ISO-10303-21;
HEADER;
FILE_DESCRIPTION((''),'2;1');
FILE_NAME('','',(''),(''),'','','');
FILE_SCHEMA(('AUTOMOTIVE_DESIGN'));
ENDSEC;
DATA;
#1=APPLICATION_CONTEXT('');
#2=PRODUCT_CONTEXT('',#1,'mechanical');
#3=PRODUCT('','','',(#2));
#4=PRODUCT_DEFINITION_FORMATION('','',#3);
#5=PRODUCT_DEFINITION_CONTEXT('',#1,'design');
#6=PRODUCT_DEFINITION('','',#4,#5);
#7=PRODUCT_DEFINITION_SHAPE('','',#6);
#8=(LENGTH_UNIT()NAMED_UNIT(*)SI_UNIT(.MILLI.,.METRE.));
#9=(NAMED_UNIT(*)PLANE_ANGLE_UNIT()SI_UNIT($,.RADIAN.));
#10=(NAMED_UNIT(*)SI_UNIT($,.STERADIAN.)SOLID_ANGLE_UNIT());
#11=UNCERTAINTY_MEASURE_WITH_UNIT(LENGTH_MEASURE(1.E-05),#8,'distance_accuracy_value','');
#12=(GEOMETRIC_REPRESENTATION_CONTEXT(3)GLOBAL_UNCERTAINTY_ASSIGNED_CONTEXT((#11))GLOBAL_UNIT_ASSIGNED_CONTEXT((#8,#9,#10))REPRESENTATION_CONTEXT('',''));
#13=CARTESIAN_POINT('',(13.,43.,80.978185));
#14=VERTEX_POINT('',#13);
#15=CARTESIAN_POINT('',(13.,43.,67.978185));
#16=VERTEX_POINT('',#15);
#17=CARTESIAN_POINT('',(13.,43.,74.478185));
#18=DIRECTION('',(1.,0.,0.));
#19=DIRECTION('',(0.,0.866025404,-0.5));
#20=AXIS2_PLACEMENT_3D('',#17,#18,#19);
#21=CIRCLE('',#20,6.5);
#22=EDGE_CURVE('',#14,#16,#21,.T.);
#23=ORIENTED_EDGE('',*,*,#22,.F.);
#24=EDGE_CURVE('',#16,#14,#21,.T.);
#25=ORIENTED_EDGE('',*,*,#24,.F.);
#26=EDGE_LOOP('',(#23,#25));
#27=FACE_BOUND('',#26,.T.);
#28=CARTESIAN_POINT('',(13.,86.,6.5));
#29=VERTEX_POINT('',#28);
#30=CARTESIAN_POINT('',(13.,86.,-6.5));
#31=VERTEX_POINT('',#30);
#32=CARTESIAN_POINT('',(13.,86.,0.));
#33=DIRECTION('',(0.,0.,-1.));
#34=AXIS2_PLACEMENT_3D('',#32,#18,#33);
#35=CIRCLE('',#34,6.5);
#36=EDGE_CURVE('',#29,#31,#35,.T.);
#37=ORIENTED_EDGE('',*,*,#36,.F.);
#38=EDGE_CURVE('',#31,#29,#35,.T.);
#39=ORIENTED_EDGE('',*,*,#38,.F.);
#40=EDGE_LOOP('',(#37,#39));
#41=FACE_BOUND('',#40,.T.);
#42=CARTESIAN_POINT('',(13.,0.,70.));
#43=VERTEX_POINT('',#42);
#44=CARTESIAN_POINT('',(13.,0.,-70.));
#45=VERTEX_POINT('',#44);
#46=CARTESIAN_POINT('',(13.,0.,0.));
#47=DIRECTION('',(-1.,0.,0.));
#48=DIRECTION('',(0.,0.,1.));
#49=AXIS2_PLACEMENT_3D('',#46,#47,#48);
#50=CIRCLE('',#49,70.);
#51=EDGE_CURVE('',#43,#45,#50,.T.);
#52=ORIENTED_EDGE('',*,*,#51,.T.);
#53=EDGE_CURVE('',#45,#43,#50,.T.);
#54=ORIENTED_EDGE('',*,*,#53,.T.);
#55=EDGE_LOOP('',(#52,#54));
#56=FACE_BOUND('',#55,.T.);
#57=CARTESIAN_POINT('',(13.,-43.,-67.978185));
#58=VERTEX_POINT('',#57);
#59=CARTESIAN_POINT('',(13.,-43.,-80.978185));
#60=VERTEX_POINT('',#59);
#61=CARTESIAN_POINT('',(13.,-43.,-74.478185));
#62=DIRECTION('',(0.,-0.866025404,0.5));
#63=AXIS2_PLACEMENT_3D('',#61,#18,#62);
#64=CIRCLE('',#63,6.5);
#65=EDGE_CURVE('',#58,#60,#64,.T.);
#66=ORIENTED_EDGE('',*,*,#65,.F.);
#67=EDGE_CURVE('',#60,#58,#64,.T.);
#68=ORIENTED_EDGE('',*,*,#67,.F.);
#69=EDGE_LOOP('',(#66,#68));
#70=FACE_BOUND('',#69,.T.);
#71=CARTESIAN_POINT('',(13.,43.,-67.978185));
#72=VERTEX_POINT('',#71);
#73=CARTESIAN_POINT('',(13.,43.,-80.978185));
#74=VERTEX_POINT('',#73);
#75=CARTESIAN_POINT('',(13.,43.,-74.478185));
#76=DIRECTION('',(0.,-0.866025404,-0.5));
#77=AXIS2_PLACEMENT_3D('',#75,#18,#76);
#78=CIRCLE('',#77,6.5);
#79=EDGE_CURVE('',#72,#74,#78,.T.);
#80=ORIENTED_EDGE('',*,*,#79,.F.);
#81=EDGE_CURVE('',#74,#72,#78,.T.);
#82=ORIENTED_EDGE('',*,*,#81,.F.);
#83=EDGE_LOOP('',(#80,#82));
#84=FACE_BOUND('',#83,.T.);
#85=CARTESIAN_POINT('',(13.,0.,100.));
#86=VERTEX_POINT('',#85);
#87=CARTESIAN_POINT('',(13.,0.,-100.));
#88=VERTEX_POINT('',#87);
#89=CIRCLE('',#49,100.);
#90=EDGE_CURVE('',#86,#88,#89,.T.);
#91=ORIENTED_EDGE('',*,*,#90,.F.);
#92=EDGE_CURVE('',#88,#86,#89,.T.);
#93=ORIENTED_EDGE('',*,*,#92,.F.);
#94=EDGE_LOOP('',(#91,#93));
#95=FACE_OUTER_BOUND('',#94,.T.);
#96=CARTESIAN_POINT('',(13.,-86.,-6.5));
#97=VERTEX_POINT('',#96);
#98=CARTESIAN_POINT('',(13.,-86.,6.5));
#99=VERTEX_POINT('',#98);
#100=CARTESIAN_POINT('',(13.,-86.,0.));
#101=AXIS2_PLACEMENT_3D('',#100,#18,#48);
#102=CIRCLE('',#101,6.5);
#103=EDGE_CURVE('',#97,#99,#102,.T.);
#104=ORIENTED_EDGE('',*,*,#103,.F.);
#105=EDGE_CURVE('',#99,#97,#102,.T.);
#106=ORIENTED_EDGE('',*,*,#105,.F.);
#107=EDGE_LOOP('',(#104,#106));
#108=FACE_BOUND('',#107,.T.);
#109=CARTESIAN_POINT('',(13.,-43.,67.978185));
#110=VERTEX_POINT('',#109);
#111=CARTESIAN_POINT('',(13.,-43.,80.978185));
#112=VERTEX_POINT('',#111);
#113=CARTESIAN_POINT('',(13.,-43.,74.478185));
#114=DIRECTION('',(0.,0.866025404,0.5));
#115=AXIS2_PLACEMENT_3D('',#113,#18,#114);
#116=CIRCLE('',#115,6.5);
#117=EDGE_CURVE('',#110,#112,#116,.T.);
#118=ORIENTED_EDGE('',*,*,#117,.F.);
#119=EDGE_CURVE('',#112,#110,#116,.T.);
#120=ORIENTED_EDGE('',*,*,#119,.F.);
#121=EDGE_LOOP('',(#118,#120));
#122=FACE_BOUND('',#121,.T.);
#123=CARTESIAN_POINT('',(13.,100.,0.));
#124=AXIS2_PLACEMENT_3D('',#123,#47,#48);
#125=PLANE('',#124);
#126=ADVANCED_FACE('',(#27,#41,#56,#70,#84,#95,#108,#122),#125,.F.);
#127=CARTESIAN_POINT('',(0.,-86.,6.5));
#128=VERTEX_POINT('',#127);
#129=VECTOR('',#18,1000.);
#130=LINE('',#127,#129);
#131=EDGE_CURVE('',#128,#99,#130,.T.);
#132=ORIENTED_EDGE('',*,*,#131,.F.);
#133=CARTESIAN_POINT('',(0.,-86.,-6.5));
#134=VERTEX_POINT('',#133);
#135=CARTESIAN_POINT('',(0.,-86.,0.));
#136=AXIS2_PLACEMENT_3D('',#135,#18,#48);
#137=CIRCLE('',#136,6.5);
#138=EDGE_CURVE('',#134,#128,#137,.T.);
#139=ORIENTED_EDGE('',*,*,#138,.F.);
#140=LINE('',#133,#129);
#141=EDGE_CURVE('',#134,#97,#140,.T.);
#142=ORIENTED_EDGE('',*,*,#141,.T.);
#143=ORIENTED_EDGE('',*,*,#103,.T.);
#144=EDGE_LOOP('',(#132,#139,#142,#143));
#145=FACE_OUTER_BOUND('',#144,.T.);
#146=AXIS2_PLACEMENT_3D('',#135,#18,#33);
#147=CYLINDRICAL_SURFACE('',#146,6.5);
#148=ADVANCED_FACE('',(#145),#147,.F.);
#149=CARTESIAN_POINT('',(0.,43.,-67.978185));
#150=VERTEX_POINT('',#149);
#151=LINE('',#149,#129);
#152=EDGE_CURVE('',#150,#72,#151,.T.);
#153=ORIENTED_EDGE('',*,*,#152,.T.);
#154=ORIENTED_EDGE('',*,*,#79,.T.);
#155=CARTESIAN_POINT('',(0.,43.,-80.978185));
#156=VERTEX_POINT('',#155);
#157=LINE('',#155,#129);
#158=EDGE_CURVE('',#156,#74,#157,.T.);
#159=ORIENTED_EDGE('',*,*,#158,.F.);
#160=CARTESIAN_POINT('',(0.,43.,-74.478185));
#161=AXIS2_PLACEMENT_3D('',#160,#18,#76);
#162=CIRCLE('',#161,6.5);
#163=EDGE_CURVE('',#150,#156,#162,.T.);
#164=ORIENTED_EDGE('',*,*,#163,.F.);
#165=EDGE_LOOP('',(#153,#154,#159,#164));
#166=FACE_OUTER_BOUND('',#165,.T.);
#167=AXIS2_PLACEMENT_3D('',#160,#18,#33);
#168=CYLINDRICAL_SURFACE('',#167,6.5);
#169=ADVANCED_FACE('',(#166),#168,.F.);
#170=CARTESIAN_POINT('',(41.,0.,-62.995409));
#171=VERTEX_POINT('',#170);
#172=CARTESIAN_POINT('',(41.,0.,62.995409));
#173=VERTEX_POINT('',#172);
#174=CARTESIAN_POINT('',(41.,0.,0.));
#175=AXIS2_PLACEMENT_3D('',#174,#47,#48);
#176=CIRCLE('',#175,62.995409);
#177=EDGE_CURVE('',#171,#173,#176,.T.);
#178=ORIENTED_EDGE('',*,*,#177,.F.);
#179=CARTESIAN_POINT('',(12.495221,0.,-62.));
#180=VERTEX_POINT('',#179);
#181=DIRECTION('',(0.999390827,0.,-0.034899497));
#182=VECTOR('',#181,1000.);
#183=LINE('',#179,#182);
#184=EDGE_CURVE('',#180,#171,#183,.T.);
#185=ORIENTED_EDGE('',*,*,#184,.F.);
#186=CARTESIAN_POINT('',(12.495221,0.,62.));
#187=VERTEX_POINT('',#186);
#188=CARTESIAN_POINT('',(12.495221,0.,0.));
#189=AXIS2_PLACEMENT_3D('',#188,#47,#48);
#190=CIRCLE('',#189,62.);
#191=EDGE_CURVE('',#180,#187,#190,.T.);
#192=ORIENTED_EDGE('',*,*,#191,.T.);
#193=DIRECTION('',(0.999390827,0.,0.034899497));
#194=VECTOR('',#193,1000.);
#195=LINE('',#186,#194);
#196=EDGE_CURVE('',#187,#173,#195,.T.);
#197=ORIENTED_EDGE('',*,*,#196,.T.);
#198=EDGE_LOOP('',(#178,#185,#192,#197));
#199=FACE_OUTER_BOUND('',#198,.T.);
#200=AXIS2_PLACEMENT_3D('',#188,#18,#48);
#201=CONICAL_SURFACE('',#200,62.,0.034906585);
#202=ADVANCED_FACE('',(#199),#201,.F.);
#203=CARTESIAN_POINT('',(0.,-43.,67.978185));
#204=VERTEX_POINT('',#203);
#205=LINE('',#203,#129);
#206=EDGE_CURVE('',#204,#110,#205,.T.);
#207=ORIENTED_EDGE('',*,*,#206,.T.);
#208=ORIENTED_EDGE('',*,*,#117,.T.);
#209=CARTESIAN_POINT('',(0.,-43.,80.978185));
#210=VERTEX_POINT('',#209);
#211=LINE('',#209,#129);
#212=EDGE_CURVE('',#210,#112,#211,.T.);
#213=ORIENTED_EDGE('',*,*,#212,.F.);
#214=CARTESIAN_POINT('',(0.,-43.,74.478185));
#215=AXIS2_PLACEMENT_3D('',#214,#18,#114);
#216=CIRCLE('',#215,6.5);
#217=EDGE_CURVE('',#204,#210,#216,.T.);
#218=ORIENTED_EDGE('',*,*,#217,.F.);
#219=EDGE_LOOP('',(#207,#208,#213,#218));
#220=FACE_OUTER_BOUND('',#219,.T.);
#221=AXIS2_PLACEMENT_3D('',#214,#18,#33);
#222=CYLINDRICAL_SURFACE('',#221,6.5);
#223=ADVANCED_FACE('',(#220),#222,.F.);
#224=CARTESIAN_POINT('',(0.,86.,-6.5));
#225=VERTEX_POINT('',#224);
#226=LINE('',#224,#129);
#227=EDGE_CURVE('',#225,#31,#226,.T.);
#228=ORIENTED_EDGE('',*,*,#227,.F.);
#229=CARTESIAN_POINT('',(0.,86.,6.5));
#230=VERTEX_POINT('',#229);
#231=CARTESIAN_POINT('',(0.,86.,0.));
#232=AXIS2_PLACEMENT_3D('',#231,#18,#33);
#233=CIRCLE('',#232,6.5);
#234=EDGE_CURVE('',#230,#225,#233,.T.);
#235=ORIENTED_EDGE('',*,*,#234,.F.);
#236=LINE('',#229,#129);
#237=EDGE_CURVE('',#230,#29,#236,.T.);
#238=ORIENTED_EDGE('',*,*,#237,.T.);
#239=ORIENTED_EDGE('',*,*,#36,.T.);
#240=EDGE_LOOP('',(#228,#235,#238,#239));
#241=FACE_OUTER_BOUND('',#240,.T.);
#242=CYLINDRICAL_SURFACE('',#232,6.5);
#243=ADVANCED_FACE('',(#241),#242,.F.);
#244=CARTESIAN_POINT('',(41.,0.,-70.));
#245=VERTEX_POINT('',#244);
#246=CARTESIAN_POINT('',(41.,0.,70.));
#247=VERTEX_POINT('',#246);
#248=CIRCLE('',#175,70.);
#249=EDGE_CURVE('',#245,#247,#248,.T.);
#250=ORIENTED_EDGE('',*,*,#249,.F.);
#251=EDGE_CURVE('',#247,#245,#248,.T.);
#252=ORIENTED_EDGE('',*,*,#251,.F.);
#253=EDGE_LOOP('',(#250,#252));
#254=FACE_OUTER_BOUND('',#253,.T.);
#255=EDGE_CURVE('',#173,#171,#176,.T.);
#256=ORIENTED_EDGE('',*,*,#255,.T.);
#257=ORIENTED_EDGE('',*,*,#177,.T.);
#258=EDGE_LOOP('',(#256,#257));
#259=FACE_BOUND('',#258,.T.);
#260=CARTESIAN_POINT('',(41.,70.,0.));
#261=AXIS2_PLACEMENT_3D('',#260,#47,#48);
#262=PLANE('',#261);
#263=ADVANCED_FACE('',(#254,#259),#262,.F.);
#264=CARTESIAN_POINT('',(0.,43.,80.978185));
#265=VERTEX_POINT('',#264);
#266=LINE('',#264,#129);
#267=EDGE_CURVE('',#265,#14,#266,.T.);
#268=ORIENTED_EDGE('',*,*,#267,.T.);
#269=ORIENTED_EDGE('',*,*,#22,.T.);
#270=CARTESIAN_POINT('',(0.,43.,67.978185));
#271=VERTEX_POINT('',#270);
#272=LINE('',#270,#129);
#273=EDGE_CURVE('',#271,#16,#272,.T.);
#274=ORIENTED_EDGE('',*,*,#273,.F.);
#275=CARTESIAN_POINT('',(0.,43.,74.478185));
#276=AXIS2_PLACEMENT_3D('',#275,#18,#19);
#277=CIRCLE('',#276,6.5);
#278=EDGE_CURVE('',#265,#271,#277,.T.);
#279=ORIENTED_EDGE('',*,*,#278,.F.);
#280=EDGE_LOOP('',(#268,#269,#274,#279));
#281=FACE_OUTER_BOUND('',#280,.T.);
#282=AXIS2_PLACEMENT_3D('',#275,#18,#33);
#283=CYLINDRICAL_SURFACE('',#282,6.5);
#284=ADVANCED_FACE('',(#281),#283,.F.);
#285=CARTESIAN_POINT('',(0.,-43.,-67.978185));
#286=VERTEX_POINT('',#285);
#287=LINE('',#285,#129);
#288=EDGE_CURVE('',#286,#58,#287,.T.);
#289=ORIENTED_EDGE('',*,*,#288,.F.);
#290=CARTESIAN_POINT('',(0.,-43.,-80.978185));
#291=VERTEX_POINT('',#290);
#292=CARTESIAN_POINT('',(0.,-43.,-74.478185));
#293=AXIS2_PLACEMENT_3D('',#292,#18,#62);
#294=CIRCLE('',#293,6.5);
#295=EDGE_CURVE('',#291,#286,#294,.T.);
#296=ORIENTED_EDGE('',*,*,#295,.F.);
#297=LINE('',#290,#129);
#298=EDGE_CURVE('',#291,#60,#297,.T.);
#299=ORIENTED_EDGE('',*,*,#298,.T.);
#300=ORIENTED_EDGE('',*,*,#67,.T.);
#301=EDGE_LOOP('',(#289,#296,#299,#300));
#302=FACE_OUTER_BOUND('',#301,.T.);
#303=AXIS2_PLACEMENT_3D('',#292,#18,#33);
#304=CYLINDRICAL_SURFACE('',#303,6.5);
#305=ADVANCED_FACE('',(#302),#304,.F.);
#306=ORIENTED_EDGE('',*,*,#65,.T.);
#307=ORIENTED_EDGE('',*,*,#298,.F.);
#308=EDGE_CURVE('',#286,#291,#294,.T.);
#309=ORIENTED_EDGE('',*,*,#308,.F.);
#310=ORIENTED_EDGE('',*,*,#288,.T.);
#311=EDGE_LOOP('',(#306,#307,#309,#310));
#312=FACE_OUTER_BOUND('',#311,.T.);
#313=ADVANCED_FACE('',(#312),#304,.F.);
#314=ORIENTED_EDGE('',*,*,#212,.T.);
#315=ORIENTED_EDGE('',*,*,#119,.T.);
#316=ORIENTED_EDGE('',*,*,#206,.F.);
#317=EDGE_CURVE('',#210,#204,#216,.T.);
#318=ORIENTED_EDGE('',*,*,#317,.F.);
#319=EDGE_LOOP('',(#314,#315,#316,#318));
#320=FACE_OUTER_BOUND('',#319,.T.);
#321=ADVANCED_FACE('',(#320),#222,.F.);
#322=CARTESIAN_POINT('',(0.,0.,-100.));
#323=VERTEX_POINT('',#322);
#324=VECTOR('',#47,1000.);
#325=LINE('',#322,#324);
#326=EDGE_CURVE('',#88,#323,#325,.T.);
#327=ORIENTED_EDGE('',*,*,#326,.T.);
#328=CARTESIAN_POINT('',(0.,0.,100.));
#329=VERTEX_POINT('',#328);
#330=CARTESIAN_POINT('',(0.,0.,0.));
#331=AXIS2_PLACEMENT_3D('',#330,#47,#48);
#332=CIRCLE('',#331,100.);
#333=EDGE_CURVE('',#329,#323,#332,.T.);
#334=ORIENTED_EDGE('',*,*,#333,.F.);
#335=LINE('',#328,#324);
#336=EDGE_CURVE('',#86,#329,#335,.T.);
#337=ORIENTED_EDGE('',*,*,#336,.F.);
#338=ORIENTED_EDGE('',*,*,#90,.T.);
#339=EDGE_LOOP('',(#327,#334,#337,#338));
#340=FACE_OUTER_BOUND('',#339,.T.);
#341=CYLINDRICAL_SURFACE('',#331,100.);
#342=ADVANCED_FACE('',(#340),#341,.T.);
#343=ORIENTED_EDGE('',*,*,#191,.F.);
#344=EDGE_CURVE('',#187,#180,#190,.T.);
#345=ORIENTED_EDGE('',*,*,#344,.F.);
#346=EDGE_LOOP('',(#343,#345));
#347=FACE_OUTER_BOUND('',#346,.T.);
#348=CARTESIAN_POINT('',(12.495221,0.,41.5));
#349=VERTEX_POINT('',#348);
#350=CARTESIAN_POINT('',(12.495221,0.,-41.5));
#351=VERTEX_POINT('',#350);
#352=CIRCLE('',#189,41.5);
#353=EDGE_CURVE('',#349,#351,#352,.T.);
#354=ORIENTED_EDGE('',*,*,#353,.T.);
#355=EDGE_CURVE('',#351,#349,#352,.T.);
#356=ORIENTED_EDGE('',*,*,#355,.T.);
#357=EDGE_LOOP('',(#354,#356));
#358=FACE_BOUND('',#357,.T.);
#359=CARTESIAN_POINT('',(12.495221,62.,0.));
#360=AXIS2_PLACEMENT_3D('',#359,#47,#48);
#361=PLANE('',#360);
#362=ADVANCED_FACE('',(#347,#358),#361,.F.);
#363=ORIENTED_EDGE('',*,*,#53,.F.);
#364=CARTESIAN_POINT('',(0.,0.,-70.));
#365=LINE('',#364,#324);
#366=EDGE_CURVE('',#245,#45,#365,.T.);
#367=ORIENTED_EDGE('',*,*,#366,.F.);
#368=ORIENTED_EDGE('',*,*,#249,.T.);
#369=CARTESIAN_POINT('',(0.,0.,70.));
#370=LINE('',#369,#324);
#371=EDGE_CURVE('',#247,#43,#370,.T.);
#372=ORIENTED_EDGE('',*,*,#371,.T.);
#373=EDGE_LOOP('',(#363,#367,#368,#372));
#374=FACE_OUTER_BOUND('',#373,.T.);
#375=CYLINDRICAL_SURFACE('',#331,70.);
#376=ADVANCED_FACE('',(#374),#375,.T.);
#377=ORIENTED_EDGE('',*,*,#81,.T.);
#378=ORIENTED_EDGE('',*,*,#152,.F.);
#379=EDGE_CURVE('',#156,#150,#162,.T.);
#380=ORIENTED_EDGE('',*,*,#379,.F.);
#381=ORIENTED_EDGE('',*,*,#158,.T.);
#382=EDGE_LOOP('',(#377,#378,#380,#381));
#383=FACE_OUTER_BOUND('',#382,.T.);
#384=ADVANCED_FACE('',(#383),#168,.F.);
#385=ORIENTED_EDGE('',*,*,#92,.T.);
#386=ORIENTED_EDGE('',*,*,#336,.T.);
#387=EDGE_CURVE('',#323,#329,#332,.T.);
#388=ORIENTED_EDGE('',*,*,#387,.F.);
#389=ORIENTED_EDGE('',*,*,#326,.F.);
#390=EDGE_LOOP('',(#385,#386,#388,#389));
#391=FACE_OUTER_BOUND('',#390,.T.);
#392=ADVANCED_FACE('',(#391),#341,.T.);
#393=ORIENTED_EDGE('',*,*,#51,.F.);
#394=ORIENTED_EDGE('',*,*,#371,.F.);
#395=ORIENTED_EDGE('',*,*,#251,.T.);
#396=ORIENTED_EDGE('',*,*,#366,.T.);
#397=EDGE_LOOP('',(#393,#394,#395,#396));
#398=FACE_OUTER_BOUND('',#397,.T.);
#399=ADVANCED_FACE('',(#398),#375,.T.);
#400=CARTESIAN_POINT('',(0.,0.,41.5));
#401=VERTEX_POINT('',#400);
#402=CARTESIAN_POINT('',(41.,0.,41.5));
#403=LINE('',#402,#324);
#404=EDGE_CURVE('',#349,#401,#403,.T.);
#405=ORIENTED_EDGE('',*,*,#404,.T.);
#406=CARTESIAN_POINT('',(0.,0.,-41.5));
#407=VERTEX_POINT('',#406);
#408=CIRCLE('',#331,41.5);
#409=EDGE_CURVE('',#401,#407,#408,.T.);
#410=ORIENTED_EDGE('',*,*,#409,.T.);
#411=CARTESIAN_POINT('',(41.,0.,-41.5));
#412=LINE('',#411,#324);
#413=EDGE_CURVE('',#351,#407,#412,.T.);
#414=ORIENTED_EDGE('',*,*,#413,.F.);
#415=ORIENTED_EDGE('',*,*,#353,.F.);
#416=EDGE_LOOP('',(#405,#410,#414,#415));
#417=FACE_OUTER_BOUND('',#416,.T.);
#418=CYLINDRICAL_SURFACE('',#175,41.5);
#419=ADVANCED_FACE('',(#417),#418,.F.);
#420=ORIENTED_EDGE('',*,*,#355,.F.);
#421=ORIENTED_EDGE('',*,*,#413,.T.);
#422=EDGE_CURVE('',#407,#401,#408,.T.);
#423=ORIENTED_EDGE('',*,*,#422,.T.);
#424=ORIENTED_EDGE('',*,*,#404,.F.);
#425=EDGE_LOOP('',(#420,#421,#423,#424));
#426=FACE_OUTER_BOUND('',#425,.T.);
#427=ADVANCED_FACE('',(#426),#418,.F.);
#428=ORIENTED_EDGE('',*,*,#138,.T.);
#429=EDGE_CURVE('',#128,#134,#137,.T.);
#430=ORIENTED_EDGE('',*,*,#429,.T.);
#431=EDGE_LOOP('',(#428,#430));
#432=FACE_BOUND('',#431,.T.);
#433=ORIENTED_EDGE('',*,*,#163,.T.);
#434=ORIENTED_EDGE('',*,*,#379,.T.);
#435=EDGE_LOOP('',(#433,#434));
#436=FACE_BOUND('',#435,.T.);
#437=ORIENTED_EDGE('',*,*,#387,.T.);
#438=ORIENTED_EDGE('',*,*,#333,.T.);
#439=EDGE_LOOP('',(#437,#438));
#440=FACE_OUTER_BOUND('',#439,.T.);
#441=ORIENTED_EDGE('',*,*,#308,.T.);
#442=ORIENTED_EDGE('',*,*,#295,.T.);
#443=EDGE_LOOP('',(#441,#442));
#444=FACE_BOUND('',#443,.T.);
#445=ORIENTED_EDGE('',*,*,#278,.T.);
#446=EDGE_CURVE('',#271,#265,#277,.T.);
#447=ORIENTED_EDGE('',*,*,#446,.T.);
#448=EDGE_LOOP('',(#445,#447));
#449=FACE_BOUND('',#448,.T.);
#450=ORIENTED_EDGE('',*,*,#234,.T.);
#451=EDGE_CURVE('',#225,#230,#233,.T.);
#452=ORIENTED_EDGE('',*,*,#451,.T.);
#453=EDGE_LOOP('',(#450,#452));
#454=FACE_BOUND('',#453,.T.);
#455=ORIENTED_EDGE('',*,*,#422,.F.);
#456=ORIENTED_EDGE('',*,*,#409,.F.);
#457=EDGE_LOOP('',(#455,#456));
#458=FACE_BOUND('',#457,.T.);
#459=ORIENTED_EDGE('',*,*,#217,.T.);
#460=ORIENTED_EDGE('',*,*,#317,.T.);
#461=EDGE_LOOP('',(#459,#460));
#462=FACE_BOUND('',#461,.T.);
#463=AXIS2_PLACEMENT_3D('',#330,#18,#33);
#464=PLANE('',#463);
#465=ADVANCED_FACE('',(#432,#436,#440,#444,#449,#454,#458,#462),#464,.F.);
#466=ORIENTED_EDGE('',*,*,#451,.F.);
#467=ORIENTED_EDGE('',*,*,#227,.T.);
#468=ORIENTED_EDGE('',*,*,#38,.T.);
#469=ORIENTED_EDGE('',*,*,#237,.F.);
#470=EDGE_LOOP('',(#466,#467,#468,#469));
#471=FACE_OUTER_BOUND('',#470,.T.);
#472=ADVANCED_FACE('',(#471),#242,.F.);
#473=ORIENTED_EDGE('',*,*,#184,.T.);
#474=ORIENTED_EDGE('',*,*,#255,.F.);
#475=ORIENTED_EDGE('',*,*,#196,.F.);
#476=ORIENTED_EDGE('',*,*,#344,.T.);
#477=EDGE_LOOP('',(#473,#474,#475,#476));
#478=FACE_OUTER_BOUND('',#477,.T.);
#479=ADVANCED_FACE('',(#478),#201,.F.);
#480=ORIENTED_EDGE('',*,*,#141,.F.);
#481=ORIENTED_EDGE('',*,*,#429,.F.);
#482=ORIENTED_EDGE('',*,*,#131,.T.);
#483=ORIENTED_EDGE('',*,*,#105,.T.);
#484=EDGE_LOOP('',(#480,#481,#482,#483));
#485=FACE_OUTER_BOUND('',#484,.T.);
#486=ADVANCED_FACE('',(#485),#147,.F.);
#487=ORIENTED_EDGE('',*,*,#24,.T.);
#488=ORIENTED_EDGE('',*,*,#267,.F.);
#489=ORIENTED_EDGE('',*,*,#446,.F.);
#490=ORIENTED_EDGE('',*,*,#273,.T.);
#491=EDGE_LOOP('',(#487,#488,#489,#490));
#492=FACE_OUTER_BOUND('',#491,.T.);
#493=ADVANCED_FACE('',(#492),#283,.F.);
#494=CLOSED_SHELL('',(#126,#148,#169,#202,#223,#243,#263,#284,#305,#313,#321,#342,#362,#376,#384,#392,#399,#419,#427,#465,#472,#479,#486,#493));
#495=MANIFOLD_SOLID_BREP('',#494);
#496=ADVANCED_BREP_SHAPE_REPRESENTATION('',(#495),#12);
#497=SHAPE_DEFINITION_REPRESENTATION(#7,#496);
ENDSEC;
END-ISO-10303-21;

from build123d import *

# Parameters (mm, degrees)
SKETCH2_R          = 6.5
CUT_EXTRUDE1_DEPTH = 145.166570328
CIRPATTERN1_COUNT  = 6
SKETCH3_R          = 41.5
CUT_EXTRUDE2_DEPTH = 148.244694302
DRAFT1_ANGLE       = 2


with BuildPart() as part:
    # Sketch1 → Revolve1 (revolve)
    with BuildSketch(Plane.XY, mode=Mode.PRIVATE) as revolve1_sk:
        Polygon((0, 0), (0, 100), (13, 100), (13, 70), (41, 70), (41, 62), (12.495221111, 62), (12.495221111, 0), align=None)
    revolve(revolve1_sk.sketch.rotate(Axis((0, 0, 0), (1, 0, 0)), 90), axis=Axis((0, 0, 0), (1, 0, 0)))

    # Sketch2 → Cut-Extrude1 (cut, through all)
    with BuildSketch(Plane(origin=(13, 0, 0), x_dir=(0, 0, -1), z_dir=(1, 0, 0))):
        with Locations((0, 86)):
            Circle(SKETCH2_R)
    cut_extrude1 = extrude(amount=-CUT_EXTRUDE1_DEPTH, mode=Mode.SUBTRACT)

    # CirPattern1: Cut-Extrude1 ×6 about axis
    cirpattern1_axis = Axis((0, 0, 0), (1, 0, 0))
    for i in range(1, CIRPATTERN1_COUNT):
        add(cut_extrude1.rotate(cirpattern1_axis, i * 360 / CIRPATTERN1_COUNT), mode=Mode.SUBTRACT)

    # Sketch3 → Cut-Extrude2 (cut, through all)
    with BuildSketch(Plane.ZY):
        Circle(SKETCH3_R)
    extrude(amount=-CUT_EXTRUDE2_DEPTH, mode=Mode.SUBTRACT)

    # Draft1
    draft1_faces = [part.faces().sort_by_distance(p)[0] for p in [
        (26.747610556, 0, -62),
    ]]
    draft(draft1_faces, Plane(origin=(12.495221111, 62, 0), x_dir=(0, 0, 1), z_dir=(1, 0, 0)), DRAFT1_ANGLE)


solid = part.part
